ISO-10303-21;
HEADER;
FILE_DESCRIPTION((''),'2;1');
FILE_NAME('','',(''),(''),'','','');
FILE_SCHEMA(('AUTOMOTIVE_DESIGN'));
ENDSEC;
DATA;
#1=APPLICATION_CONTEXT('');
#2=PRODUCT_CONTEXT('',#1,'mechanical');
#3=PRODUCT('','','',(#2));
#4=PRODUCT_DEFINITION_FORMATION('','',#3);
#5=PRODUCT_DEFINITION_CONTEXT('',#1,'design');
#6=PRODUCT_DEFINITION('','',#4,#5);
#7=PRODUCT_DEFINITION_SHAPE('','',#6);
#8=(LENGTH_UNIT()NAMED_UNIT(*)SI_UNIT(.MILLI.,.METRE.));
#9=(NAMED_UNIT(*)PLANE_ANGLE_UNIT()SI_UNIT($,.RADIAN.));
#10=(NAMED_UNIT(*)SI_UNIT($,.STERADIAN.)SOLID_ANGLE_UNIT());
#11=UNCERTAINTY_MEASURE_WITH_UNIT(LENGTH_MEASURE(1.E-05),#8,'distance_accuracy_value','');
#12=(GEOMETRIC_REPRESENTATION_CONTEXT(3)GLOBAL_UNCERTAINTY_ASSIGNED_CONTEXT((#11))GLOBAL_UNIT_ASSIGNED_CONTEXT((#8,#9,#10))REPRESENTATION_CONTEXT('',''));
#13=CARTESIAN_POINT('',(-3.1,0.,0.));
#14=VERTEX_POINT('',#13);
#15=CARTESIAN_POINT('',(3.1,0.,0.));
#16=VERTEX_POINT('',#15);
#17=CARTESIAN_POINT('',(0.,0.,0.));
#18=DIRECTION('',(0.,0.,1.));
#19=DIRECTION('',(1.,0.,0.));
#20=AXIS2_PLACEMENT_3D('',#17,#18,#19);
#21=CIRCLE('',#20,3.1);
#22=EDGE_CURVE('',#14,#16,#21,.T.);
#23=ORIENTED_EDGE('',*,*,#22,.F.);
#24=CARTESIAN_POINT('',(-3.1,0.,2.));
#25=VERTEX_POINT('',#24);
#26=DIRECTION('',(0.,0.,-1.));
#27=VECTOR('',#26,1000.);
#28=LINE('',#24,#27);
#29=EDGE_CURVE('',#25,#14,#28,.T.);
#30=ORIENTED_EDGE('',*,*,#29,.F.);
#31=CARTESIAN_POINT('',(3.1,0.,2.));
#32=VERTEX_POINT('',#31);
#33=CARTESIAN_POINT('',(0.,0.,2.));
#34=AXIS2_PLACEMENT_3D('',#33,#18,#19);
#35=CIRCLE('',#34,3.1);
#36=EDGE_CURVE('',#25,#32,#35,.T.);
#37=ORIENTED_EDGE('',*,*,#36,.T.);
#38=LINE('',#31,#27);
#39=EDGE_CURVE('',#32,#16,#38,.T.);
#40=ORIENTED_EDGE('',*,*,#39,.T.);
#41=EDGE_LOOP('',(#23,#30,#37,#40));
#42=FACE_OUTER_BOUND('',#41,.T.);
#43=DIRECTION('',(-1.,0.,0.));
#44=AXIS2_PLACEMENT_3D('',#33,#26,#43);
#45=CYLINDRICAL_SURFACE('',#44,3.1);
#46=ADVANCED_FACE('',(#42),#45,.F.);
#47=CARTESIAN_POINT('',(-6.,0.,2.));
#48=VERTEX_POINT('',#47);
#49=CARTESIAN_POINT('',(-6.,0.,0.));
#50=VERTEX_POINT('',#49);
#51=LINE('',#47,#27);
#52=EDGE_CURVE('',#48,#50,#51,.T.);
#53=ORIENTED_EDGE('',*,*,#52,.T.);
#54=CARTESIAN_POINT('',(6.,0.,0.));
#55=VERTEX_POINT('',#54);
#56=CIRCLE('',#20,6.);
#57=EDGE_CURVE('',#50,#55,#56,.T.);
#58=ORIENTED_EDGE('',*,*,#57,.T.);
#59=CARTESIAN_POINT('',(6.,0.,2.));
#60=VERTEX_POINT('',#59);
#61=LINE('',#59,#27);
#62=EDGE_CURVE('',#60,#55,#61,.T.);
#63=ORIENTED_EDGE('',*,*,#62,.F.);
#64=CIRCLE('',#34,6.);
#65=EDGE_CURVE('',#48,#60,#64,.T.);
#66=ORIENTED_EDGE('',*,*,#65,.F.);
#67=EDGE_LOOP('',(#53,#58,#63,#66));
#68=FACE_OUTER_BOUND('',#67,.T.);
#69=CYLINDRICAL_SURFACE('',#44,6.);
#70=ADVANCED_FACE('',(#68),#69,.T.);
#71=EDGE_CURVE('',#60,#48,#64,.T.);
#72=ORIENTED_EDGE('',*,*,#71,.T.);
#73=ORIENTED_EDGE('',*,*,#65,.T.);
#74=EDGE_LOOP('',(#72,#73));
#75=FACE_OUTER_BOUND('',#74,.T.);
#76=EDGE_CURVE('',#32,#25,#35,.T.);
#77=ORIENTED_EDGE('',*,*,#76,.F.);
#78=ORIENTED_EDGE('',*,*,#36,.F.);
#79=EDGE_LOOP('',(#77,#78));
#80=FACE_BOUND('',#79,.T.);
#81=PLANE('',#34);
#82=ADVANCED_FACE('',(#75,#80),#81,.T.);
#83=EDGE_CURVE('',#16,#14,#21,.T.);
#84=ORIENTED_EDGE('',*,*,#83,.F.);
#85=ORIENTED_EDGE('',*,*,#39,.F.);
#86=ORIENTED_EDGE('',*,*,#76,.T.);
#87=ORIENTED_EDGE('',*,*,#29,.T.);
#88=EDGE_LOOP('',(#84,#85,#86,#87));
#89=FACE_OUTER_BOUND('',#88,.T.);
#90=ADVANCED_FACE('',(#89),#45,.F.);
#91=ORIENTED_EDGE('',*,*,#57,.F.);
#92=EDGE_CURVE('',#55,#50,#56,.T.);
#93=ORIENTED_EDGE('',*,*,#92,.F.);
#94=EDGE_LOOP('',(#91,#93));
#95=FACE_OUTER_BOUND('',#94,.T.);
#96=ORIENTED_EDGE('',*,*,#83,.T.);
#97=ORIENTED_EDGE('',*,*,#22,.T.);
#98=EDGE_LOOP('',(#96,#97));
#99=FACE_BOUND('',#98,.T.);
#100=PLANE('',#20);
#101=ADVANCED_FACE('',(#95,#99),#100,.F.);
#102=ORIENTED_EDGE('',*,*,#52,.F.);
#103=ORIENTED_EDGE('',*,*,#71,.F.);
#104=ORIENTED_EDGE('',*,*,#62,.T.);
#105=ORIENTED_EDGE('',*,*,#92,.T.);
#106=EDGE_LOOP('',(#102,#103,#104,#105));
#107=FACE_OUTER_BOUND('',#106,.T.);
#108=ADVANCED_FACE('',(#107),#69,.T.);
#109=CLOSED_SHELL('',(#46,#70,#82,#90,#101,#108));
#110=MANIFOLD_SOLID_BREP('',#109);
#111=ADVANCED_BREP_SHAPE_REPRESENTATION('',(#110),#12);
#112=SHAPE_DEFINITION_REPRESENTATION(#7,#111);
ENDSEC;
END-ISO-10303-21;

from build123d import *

# Parameters (mm, degrees)
SKETCH1_R      = 6
SKETCH1_R_2    = 3.1
EXTRUDE1_DEPTH = 2


with BuildPart() as part:
    # Sketch1 → Extrude1 (new body)
    with BuildSketch(Plane.XY):
        Circle(SKETCH1_R)
        Circle(SKETCH1_R_2, mode=Mode.SUBTRACT)
    extrude(amount=EXTRUDE1_DEPTH)


solid = part.part
